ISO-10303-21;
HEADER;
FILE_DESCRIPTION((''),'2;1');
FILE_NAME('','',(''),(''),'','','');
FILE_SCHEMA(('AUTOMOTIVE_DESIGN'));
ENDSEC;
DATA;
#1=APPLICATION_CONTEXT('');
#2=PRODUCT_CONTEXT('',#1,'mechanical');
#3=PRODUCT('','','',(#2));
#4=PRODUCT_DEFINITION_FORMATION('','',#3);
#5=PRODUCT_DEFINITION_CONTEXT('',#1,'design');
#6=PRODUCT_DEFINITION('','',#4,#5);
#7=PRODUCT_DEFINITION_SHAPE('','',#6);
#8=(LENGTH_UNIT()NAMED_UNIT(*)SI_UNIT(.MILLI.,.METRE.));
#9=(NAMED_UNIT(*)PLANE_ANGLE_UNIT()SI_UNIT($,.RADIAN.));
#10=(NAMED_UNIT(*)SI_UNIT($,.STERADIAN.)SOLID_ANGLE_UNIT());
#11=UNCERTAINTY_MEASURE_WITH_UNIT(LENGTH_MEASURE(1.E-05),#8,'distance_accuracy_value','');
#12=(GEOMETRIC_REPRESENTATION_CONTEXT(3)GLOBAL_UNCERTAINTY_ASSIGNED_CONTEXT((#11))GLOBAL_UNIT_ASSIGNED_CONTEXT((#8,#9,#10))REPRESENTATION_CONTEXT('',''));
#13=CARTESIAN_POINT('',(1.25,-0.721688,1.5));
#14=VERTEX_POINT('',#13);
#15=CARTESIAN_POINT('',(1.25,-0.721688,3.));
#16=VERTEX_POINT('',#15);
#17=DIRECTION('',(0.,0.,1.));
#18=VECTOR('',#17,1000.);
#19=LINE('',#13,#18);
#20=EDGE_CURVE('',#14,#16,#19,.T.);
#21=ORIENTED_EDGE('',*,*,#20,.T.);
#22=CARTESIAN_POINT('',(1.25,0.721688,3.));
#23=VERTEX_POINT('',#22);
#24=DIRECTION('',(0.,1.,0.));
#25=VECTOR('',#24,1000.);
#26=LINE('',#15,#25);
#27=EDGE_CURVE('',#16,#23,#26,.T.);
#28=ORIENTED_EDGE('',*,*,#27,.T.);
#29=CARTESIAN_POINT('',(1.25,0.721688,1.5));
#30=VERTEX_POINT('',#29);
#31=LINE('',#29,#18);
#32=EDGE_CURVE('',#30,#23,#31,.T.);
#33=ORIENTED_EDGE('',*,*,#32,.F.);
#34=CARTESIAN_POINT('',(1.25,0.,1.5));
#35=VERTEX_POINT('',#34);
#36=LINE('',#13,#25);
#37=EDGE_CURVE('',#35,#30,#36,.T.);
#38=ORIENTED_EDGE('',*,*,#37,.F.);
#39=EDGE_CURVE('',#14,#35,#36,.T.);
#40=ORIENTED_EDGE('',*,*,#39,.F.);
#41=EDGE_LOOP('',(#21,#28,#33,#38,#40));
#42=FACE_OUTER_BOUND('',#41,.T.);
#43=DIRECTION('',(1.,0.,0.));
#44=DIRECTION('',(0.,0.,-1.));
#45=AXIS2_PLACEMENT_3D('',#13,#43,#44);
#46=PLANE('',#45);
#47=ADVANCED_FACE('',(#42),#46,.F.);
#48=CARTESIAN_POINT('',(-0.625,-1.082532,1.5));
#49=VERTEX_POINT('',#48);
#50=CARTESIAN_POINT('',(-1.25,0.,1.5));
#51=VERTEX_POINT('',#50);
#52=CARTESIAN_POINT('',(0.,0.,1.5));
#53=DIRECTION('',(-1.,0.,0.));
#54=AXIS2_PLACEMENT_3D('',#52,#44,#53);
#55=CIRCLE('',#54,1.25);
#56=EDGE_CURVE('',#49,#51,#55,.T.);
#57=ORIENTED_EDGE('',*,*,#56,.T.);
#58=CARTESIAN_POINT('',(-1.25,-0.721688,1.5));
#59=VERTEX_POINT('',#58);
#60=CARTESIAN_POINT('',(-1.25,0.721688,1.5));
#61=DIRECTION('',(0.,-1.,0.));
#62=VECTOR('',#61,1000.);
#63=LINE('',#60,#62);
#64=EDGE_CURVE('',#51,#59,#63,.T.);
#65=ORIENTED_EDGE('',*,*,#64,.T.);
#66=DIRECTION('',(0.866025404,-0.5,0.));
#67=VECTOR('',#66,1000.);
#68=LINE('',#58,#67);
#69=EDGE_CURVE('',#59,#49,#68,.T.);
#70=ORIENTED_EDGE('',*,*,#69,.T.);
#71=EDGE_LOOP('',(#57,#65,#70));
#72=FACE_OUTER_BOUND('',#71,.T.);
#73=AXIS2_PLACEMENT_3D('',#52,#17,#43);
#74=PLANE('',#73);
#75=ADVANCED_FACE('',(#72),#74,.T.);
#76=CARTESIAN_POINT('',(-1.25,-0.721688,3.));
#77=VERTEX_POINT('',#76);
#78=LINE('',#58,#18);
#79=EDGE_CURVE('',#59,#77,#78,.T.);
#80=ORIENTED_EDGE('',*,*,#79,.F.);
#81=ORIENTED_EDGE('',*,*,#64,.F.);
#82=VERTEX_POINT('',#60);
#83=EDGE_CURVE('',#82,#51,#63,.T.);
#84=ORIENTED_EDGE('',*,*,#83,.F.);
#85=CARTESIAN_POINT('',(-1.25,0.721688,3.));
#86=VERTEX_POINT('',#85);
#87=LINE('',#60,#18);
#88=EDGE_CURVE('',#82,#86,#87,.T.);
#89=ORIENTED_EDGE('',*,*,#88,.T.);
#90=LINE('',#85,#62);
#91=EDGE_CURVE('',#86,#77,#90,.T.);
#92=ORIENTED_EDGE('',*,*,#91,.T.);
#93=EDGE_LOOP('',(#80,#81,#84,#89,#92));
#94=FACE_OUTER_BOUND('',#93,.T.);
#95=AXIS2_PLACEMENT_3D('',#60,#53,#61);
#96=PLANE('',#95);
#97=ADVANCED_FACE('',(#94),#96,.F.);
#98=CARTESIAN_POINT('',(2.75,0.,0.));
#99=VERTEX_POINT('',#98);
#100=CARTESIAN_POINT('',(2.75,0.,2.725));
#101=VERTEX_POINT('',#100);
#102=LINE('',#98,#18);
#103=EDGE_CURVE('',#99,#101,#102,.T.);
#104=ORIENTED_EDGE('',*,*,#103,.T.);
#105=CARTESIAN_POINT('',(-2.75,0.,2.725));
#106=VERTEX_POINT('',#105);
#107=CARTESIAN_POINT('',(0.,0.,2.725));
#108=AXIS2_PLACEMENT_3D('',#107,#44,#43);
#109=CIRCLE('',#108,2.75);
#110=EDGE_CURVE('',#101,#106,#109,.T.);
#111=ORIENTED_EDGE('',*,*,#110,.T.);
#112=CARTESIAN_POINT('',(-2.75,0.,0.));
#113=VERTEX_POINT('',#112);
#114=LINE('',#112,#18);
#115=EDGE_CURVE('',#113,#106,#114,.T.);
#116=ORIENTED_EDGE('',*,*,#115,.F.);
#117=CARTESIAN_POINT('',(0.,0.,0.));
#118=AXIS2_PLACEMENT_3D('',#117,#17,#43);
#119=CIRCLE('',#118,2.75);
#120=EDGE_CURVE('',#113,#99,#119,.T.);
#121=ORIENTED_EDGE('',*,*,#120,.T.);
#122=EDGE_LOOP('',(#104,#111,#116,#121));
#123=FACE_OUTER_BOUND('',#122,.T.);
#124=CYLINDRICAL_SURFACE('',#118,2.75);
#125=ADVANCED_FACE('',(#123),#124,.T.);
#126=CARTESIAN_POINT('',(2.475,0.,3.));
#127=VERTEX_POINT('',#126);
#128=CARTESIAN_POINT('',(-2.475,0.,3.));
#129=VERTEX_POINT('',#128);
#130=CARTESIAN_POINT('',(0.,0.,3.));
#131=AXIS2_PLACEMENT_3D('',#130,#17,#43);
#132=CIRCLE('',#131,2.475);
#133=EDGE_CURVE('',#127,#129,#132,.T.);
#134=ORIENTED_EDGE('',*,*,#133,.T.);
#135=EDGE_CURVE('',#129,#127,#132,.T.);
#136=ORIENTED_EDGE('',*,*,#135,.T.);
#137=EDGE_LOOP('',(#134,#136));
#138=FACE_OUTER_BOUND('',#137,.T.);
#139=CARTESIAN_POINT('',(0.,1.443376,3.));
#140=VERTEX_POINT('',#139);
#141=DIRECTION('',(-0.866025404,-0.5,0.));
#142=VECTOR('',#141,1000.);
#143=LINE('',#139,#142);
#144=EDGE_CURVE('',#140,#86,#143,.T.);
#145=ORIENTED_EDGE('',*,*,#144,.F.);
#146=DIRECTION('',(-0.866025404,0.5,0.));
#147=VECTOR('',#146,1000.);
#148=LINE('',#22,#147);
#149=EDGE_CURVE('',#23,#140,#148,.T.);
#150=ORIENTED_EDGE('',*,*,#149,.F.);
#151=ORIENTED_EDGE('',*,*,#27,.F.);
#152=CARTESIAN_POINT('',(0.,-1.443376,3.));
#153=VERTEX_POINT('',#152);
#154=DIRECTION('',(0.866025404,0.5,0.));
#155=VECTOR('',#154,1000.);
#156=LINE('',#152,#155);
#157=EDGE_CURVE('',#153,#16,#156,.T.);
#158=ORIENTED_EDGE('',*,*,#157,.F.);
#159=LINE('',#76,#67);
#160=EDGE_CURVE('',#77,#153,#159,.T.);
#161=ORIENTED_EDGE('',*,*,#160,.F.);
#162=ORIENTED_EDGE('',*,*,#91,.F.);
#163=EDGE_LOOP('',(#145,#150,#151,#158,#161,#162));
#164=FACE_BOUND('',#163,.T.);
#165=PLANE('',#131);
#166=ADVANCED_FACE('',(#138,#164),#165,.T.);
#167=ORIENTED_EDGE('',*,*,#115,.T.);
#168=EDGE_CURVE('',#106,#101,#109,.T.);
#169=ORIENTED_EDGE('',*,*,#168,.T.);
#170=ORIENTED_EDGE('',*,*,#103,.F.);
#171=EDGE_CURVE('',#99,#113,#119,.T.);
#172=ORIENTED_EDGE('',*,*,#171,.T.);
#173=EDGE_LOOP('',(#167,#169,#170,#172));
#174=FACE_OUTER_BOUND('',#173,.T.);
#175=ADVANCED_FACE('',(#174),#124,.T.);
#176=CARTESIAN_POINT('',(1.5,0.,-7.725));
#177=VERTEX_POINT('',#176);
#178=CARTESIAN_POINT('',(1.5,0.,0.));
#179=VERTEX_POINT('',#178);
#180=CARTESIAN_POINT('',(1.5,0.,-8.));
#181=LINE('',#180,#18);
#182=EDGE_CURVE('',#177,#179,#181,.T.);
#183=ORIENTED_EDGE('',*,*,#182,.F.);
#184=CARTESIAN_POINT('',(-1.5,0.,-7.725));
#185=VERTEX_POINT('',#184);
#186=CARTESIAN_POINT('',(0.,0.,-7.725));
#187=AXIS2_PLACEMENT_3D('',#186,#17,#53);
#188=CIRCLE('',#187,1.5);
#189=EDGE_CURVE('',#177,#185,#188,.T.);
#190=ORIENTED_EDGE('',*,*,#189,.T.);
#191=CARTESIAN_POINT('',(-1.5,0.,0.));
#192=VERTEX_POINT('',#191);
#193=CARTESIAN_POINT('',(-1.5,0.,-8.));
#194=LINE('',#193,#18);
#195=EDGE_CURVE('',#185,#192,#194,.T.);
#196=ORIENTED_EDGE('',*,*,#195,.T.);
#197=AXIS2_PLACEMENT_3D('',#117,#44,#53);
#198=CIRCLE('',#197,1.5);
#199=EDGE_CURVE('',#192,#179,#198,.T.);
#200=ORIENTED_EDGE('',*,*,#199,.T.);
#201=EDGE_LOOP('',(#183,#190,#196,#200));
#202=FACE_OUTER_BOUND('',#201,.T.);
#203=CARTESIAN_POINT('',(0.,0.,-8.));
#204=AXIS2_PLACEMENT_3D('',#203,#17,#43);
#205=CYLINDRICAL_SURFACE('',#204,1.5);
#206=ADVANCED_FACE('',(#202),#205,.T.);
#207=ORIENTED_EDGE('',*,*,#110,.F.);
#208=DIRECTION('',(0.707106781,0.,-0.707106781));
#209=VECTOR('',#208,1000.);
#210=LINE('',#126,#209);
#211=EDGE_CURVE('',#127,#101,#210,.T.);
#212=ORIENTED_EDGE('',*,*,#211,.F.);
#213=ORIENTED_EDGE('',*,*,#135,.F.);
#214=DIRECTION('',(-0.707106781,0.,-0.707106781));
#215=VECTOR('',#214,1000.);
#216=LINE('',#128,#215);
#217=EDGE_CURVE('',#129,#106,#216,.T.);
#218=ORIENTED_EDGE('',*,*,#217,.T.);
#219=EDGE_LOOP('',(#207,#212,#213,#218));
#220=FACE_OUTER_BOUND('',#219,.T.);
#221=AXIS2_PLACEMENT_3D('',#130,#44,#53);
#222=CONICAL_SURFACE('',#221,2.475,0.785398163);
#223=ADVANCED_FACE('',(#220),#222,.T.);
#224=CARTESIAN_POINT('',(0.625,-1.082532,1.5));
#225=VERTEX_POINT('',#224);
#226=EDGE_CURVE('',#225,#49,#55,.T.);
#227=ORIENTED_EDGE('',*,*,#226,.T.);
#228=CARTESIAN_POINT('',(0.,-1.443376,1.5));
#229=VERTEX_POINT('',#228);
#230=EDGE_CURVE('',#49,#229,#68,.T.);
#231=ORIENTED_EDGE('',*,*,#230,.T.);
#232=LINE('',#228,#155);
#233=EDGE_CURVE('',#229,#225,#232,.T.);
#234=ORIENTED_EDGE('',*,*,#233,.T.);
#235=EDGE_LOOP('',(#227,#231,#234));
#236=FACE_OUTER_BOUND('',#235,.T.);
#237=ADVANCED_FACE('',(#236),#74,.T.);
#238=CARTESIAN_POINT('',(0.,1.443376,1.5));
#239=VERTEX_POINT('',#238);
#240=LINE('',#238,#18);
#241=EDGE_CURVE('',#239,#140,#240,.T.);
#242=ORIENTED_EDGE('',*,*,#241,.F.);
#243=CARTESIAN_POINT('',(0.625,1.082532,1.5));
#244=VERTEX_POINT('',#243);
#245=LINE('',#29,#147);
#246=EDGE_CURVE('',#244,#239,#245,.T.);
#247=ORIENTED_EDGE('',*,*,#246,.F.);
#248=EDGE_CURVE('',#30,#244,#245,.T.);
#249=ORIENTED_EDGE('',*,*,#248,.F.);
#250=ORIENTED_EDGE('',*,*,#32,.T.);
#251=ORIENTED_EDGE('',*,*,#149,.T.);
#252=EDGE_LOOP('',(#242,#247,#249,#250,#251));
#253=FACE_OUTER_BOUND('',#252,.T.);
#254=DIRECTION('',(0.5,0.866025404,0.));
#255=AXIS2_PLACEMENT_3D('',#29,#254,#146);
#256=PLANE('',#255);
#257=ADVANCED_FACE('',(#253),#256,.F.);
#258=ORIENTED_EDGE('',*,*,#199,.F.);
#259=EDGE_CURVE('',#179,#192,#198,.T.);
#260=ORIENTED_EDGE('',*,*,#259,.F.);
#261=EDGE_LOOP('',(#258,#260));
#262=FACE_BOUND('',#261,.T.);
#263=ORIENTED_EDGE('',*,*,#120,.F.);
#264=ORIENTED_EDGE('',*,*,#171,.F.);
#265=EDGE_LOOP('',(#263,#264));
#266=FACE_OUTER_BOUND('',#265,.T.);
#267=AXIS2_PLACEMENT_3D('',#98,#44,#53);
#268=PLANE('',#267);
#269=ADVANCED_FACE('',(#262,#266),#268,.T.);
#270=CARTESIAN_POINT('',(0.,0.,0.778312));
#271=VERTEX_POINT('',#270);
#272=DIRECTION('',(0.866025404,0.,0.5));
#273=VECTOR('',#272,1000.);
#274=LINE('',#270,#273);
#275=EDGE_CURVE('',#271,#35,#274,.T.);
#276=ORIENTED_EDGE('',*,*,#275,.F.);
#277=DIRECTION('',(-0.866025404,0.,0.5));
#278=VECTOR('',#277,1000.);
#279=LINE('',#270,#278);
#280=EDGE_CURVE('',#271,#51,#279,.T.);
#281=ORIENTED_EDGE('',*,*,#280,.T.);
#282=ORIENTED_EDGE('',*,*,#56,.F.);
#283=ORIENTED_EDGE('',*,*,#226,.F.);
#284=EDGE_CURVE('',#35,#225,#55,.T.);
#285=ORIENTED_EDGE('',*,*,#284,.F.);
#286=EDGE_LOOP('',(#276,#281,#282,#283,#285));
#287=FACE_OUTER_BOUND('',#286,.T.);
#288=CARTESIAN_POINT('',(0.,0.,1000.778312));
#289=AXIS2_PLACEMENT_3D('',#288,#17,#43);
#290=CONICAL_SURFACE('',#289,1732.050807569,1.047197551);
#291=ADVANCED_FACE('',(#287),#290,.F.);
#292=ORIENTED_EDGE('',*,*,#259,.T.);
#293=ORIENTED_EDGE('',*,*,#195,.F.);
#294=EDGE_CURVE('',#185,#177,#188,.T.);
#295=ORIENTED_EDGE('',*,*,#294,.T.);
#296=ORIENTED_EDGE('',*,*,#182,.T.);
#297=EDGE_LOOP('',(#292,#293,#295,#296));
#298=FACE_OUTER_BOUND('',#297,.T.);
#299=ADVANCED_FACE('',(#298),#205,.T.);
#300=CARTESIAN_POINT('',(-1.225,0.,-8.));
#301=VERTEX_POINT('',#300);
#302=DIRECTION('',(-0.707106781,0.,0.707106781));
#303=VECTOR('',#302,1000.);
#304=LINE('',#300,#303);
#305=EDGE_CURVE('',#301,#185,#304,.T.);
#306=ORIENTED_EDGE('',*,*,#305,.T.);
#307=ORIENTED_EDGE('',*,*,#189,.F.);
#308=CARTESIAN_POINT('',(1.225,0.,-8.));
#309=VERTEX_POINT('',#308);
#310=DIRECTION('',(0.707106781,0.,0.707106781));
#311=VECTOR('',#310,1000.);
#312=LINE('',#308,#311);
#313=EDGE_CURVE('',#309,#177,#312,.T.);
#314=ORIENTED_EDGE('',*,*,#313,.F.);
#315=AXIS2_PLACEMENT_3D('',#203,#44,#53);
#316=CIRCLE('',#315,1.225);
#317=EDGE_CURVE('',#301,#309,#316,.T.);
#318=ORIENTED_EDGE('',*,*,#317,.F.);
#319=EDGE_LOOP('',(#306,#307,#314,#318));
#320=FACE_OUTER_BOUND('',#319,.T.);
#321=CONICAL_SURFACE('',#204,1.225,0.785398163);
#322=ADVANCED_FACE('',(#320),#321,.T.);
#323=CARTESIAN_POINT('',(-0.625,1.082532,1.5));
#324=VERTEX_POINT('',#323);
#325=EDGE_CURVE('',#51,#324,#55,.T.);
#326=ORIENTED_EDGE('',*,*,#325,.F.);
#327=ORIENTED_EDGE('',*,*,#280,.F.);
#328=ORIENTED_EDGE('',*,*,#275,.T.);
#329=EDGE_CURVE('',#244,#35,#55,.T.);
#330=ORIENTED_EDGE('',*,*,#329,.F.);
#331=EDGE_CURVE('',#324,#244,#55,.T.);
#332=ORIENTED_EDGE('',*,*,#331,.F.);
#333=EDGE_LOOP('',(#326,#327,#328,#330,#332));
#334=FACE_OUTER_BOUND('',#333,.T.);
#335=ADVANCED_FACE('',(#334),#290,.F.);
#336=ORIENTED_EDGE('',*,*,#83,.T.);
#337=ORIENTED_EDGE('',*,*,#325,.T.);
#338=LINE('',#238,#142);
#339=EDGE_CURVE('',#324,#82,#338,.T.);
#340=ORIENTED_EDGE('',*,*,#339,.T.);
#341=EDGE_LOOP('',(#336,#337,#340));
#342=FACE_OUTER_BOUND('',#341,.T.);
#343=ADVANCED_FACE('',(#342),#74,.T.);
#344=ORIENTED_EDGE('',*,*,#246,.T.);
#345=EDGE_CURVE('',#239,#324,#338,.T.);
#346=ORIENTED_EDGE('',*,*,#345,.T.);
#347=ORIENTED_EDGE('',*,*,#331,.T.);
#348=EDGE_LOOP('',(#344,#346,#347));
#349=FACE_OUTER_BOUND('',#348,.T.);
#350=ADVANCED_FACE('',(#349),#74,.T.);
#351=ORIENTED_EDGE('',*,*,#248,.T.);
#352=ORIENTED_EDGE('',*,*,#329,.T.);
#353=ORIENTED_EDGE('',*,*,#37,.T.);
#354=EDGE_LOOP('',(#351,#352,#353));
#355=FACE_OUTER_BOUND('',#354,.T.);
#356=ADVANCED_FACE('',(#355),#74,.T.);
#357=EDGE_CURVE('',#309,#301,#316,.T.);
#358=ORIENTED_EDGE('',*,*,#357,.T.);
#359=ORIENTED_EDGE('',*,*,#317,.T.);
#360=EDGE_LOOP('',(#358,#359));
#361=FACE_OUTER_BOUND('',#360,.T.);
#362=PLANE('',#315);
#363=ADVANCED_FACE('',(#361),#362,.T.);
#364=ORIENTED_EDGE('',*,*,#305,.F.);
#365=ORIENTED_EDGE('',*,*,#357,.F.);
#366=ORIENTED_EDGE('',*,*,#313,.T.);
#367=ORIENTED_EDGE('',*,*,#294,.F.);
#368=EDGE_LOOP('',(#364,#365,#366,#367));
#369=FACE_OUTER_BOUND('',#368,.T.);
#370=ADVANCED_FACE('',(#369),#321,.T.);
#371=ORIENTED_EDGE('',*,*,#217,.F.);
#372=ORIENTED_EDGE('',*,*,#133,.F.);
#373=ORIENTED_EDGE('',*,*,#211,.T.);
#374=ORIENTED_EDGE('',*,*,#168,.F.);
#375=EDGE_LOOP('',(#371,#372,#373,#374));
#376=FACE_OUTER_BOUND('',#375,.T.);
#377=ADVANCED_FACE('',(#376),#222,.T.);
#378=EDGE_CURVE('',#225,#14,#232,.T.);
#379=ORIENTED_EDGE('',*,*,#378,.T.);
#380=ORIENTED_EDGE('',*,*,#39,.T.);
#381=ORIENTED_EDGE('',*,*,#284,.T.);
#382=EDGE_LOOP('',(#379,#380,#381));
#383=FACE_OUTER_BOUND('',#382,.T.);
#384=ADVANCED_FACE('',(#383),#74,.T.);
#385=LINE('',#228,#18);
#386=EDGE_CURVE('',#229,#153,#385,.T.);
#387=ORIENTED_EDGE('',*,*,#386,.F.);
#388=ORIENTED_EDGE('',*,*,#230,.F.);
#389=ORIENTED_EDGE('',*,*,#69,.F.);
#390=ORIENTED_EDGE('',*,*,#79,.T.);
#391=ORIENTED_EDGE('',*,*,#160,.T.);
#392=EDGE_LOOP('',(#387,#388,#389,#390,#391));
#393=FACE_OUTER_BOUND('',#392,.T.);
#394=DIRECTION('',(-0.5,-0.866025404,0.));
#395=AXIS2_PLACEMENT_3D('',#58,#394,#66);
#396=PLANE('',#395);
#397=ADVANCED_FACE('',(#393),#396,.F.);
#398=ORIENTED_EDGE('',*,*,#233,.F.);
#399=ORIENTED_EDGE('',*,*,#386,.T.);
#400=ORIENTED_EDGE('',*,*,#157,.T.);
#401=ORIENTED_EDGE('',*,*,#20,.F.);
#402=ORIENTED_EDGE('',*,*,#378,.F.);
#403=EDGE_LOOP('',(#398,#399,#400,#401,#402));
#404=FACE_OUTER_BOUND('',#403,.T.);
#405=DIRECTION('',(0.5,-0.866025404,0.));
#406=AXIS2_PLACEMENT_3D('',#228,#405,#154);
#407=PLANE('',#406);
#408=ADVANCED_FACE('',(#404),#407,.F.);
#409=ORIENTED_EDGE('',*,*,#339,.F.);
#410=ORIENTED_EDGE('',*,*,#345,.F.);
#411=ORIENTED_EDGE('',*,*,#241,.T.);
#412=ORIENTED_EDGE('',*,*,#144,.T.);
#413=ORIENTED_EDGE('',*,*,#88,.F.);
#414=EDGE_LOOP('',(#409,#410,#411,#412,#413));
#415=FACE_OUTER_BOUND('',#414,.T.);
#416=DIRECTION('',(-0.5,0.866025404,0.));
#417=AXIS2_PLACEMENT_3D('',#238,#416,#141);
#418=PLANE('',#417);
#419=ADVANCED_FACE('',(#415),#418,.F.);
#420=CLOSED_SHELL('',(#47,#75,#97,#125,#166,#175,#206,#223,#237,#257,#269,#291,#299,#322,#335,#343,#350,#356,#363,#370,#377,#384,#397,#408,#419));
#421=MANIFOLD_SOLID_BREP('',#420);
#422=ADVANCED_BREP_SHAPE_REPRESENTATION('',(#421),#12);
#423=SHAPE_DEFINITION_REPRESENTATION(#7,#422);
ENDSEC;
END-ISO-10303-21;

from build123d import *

# Parameters (mm, degrees)
SKETCH_1_W          = 2.75
SKETCH_1_H          = 3
SKETCH_2_R          = 1.5
EXTRUDE_1_DEPTH     = 8
CUT_EXTRUDE_1_DEPTH = 1.5
CHAMFER_1_SIZE      = 0.275


with BuildPart() as part:
    # 草图1 → 旋转1 (revolve)
    with BuildSketch(Plane(origin=(0, 0, 0), x_dir=(1, 0, 0), z_dir=(0, 1, 0))):
        with Locations((1.375, -1.5)):
            Rectangle(SKETCH_1_W, SKETCH_1_H)
    revolve(axis=Axis((0, 0, 0), (0, 0, 1)))

    # 草图2 → 凸台-拉伸1 (add)
    with BuildSketch(Plane(origin=(0, 0, 0), x_dir=(-1, 0, 0), z_dir=(0, 0, -1))):
        Circle(SKETCH_2_R)
    extrude(amount=EXTRUDE_1_DEPTH)

    # 草图3 → 切除-拉伸1 (cut)
    with BuildSketch(Plane.XY.offset(3)):
        Polygon((1.25, -0.721687836), (1.25, 0.721687836), (0, 1.443375673), (-1.25, 0.721687836), (-1.25, -0.721687836), (0, -1.443375673), align=None)
    extrude(amount=-CUT_EXTRUDE_1_DEPTH, mode=Mode.SUBTRACT)

    # 草图4 → 切除-旋转1 (revolve, cut)
    with BuildSketch(Plane.XZ):
        Polygon((1.25, 1.5), (0, 1.5), (0, 0.778312164), align=None)
    revolve(axis=Axis((0, 0, 1.5), (0, 0, -1)), mode=Mode.SUBTRACT)

    # 倒角1
    chamfer_1_edges = [part.edges().sort_by_distance(p)[0] for p in [
        (-2.75, 0, 3),
        (1.5, 0, -8),
    ]]
    chamfer(chamfer_1_edges, length=CHAMFER_1_SIZE)


solid = part.part
